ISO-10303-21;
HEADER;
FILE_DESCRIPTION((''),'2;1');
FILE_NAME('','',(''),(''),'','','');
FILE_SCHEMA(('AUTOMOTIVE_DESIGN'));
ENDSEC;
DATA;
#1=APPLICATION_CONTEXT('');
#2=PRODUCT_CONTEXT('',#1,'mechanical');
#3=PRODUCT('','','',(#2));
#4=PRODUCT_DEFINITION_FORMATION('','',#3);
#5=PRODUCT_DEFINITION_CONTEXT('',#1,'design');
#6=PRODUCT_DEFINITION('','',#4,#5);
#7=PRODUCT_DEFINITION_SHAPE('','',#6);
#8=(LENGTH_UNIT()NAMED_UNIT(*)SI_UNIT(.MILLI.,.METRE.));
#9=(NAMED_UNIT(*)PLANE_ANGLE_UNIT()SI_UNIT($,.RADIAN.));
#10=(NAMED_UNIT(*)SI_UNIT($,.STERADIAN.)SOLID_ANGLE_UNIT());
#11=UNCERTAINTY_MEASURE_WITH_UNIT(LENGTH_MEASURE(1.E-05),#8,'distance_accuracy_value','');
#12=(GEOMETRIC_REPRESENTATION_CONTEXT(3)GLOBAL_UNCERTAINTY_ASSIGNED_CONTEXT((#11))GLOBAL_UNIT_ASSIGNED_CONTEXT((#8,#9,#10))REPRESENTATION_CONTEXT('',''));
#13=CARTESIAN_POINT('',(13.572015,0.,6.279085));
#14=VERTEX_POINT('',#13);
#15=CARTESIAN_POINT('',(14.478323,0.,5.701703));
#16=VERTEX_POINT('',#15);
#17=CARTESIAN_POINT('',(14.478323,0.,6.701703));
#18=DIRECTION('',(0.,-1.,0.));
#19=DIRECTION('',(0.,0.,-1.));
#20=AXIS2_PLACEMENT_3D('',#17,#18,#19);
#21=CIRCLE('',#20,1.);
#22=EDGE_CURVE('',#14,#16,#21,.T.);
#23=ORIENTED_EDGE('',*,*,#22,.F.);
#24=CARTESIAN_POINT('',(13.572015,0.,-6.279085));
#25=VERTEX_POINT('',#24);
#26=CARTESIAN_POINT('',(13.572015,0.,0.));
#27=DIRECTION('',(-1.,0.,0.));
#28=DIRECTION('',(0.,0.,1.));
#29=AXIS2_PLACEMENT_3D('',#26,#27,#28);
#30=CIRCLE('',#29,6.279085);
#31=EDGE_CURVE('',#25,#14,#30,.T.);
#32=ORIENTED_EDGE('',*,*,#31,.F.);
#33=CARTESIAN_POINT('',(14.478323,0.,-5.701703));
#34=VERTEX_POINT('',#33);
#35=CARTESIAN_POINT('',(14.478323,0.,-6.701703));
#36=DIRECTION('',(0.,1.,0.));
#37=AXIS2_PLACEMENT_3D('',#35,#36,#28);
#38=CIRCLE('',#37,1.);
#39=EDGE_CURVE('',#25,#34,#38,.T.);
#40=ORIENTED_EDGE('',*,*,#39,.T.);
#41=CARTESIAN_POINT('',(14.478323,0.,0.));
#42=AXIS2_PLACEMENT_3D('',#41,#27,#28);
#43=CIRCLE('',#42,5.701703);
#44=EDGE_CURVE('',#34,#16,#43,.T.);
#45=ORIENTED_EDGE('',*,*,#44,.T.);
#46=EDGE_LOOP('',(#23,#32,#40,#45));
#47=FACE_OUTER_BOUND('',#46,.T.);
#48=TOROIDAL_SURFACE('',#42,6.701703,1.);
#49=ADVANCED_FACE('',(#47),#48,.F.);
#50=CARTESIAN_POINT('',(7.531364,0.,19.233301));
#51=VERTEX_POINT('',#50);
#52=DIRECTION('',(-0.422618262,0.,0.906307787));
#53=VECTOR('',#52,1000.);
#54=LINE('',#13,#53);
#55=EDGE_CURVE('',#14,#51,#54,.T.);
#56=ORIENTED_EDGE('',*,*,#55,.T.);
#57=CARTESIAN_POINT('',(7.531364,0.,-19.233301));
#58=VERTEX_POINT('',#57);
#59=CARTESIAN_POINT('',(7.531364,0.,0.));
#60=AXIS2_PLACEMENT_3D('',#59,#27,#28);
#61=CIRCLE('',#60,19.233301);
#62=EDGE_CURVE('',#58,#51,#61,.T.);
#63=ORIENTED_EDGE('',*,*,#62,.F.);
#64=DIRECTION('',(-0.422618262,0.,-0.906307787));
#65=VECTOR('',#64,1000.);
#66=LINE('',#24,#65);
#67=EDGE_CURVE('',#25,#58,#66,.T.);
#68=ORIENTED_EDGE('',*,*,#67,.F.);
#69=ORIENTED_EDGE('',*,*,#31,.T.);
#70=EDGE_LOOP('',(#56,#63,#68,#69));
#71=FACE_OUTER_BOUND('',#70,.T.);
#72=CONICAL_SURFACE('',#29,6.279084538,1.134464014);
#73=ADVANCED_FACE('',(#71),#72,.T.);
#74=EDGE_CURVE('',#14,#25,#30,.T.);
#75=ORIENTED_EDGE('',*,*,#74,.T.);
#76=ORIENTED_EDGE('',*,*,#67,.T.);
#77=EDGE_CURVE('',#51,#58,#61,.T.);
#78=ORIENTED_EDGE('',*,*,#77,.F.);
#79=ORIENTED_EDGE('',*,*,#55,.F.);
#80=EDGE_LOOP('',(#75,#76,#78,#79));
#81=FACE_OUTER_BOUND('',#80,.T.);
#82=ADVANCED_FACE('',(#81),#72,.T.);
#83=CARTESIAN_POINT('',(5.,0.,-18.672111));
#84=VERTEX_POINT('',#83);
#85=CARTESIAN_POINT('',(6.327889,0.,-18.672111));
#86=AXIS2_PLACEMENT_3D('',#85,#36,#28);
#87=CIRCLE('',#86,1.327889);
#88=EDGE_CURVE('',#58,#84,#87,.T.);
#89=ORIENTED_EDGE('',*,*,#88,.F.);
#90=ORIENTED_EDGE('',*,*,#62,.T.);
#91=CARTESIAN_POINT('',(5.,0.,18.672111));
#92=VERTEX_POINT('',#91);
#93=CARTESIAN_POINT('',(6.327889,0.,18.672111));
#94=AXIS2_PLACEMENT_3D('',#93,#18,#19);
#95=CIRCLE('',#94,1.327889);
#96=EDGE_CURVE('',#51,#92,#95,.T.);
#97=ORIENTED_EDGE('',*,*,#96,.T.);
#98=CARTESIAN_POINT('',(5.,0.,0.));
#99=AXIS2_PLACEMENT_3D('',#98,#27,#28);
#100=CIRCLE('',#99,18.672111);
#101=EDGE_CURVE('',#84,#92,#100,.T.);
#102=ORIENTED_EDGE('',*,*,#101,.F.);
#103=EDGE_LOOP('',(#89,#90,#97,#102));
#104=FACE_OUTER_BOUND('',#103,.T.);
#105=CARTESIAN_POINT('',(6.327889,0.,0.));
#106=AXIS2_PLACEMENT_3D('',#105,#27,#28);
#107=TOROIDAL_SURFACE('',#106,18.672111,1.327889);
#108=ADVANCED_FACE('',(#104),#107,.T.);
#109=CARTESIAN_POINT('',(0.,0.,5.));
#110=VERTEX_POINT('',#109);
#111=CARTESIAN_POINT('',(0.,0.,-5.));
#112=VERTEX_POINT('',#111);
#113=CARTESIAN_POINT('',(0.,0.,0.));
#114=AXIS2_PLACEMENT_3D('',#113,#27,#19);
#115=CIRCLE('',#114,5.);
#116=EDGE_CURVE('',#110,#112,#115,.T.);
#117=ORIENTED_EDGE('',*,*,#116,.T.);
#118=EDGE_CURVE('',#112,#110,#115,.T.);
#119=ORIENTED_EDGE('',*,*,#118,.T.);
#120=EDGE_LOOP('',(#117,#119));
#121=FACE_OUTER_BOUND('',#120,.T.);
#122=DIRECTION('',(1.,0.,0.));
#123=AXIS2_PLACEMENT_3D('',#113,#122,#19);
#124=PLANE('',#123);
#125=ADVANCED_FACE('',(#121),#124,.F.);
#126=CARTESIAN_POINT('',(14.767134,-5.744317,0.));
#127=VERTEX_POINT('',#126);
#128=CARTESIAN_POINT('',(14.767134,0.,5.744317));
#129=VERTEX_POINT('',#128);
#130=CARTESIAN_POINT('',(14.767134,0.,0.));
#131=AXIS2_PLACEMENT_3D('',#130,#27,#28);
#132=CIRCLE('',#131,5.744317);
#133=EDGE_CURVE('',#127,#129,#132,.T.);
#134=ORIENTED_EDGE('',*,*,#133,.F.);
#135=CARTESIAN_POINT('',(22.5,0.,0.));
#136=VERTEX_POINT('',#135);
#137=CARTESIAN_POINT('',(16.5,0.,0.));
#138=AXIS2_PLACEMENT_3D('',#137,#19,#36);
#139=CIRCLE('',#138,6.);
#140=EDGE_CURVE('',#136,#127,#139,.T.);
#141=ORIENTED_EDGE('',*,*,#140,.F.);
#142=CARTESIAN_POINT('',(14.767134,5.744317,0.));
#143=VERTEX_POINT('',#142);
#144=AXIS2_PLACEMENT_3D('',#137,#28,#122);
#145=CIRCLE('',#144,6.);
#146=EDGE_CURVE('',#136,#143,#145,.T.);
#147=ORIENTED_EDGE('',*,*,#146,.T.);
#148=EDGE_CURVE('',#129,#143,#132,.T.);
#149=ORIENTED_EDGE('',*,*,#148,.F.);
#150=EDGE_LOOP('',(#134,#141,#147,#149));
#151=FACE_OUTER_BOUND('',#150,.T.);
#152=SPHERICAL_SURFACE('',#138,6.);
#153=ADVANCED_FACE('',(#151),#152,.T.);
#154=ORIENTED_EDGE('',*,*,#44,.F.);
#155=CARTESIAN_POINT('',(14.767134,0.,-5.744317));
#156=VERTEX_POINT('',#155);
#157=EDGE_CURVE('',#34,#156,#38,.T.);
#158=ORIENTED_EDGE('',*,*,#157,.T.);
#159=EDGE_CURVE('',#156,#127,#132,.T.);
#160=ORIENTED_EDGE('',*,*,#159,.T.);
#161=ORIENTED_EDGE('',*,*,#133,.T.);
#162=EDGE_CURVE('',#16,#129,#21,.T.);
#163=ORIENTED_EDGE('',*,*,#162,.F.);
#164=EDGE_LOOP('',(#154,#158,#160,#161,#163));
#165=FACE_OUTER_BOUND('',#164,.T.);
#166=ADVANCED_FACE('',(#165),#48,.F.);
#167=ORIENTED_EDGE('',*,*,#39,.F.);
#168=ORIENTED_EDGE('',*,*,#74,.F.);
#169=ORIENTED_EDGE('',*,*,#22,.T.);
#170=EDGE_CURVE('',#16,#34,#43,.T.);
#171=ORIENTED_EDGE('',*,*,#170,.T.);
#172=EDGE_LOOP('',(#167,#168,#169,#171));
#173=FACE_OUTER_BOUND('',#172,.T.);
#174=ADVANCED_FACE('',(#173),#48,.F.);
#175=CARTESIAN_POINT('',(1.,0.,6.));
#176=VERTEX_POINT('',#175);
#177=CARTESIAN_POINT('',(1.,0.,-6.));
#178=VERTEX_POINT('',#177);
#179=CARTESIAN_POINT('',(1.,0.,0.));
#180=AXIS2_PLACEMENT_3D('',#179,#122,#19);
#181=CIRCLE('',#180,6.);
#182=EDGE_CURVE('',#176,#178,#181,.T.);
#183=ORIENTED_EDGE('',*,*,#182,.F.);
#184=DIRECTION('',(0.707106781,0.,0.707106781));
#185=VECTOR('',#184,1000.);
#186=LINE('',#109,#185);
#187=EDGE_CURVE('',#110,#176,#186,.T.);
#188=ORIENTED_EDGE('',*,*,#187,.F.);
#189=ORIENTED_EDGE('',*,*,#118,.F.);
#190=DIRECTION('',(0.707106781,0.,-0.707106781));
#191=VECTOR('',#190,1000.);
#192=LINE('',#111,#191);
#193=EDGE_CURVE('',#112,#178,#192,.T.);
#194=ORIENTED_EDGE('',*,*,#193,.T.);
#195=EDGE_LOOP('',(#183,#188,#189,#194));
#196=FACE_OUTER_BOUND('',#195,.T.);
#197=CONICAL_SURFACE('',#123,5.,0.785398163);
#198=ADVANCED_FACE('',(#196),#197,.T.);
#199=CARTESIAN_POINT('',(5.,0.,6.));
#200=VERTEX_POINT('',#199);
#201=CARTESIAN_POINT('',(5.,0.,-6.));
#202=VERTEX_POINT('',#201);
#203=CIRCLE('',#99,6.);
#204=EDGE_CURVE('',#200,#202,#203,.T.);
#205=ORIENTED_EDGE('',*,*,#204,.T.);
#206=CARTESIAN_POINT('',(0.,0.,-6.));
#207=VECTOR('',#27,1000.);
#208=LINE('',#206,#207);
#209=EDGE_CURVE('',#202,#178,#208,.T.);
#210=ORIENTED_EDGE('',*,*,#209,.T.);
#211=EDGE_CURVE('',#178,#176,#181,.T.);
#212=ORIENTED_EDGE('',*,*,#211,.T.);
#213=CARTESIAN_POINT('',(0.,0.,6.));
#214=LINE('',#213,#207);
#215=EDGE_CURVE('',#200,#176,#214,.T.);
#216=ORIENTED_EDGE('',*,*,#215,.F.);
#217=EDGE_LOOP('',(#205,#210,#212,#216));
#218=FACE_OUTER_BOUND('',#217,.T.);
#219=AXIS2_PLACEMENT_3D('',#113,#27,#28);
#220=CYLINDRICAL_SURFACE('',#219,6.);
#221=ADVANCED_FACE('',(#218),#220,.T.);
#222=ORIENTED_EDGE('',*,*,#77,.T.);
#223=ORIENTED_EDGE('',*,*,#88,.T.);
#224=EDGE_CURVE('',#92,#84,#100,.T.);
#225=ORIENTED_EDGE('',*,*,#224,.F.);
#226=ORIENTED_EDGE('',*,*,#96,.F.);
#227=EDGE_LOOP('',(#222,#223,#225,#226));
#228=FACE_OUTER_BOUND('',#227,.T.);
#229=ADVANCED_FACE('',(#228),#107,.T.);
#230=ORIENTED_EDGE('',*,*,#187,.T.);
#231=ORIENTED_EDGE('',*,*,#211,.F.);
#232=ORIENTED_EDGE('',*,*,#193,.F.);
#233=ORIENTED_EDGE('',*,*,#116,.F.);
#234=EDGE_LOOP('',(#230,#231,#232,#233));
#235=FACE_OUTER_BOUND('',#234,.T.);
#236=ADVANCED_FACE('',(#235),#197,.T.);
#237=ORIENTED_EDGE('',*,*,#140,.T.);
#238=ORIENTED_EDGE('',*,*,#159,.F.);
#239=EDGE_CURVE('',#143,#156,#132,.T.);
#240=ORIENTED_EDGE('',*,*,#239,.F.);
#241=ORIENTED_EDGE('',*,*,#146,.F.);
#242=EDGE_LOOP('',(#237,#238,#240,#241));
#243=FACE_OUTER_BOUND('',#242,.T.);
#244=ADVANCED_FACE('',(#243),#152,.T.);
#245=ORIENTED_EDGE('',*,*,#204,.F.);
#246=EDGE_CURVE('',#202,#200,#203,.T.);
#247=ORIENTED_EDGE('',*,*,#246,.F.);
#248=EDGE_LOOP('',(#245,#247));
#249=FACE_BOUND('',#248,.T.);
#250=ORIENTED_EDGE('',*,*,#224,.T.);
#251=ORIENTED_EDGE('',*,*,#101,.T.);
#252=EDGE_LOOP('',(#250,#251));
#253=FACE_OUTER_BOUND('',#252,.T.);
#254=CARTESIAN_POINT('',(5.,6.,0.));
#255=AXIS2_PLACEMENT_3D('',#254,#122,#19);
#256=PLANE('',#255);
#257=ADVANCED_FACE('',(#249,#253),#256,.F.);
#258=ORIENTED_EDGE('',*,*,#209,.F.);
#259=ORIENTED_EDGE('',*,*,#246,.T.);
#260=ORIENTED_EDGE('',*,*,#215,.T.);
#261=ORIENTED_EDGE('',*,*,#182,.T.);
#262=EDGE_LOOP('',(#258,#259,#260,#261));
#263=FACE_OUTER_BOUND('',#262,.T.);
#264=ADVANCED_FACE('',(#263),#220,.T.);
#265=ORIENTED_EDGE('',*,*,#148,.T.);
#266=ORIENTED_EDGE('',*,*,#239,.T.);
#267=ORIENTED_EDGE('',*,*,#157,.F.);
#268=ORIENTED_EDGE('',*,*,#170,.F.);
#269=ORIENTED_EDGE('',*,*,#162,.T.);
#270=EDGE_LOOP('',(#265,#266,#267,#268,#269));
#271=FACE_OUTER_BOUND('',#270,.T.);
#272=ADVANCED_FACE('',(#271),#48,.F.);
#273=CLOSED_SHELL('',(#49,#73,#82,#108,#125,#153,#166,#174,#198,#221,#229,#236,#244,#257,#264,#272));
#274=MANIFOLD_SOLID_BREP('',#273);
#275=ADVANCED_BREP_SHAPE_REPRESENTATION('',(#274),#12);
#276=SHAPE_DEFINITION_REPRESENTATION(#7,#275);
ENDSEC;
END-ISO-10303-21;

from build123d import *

# Parameters (mm, degrees)
CHAMFER1_SIZE = 1


with BuildPart() as part:
    # Sketch1 → Revolve1 (revolve)
    with BuildSketch(Plane.XY, mode=Mode.PRIVATE) as revolve1_sk:
        with BuildLine():
            Line((0, 0), (0, 6))
            Line((0, 6), (5, 6))
            Line((5, 6), (5, 18.672111461))
            ThreePointArc((5, 18.672111461), (6.040480856, 19.96852374), (7.531364262, 19.233301407))
            Line((7.531364262, 19.233301407), (13.572014794, 6.279084538))
            ThreePointArc((13.572014794, 6.279084538), (14.069886887, 5.788915703), (14.767133641, 5.744316685))
            ThreePointArc((14.767133641, 5.744316685), (20.077904543, 4.816492404), (22.5, 0))
            Line((22.5, 0), (0, 0))
        make_face()
    revolve(revolve1_sk.sketch.rotate(Axis((0, 0, 0), (1, 0, 0)), 90), axis=Axis((0, 0, 0), (1, 0, 0)))

    # Chamfer1
    chamfer1_edges = [part.edges().sort_by_distance(p)[0] for p in [
        (0, 0, -6),
    ]]
    chamfer(chamfer1_edges, length=CHAMFER1_SIZE)


solid = part.part
